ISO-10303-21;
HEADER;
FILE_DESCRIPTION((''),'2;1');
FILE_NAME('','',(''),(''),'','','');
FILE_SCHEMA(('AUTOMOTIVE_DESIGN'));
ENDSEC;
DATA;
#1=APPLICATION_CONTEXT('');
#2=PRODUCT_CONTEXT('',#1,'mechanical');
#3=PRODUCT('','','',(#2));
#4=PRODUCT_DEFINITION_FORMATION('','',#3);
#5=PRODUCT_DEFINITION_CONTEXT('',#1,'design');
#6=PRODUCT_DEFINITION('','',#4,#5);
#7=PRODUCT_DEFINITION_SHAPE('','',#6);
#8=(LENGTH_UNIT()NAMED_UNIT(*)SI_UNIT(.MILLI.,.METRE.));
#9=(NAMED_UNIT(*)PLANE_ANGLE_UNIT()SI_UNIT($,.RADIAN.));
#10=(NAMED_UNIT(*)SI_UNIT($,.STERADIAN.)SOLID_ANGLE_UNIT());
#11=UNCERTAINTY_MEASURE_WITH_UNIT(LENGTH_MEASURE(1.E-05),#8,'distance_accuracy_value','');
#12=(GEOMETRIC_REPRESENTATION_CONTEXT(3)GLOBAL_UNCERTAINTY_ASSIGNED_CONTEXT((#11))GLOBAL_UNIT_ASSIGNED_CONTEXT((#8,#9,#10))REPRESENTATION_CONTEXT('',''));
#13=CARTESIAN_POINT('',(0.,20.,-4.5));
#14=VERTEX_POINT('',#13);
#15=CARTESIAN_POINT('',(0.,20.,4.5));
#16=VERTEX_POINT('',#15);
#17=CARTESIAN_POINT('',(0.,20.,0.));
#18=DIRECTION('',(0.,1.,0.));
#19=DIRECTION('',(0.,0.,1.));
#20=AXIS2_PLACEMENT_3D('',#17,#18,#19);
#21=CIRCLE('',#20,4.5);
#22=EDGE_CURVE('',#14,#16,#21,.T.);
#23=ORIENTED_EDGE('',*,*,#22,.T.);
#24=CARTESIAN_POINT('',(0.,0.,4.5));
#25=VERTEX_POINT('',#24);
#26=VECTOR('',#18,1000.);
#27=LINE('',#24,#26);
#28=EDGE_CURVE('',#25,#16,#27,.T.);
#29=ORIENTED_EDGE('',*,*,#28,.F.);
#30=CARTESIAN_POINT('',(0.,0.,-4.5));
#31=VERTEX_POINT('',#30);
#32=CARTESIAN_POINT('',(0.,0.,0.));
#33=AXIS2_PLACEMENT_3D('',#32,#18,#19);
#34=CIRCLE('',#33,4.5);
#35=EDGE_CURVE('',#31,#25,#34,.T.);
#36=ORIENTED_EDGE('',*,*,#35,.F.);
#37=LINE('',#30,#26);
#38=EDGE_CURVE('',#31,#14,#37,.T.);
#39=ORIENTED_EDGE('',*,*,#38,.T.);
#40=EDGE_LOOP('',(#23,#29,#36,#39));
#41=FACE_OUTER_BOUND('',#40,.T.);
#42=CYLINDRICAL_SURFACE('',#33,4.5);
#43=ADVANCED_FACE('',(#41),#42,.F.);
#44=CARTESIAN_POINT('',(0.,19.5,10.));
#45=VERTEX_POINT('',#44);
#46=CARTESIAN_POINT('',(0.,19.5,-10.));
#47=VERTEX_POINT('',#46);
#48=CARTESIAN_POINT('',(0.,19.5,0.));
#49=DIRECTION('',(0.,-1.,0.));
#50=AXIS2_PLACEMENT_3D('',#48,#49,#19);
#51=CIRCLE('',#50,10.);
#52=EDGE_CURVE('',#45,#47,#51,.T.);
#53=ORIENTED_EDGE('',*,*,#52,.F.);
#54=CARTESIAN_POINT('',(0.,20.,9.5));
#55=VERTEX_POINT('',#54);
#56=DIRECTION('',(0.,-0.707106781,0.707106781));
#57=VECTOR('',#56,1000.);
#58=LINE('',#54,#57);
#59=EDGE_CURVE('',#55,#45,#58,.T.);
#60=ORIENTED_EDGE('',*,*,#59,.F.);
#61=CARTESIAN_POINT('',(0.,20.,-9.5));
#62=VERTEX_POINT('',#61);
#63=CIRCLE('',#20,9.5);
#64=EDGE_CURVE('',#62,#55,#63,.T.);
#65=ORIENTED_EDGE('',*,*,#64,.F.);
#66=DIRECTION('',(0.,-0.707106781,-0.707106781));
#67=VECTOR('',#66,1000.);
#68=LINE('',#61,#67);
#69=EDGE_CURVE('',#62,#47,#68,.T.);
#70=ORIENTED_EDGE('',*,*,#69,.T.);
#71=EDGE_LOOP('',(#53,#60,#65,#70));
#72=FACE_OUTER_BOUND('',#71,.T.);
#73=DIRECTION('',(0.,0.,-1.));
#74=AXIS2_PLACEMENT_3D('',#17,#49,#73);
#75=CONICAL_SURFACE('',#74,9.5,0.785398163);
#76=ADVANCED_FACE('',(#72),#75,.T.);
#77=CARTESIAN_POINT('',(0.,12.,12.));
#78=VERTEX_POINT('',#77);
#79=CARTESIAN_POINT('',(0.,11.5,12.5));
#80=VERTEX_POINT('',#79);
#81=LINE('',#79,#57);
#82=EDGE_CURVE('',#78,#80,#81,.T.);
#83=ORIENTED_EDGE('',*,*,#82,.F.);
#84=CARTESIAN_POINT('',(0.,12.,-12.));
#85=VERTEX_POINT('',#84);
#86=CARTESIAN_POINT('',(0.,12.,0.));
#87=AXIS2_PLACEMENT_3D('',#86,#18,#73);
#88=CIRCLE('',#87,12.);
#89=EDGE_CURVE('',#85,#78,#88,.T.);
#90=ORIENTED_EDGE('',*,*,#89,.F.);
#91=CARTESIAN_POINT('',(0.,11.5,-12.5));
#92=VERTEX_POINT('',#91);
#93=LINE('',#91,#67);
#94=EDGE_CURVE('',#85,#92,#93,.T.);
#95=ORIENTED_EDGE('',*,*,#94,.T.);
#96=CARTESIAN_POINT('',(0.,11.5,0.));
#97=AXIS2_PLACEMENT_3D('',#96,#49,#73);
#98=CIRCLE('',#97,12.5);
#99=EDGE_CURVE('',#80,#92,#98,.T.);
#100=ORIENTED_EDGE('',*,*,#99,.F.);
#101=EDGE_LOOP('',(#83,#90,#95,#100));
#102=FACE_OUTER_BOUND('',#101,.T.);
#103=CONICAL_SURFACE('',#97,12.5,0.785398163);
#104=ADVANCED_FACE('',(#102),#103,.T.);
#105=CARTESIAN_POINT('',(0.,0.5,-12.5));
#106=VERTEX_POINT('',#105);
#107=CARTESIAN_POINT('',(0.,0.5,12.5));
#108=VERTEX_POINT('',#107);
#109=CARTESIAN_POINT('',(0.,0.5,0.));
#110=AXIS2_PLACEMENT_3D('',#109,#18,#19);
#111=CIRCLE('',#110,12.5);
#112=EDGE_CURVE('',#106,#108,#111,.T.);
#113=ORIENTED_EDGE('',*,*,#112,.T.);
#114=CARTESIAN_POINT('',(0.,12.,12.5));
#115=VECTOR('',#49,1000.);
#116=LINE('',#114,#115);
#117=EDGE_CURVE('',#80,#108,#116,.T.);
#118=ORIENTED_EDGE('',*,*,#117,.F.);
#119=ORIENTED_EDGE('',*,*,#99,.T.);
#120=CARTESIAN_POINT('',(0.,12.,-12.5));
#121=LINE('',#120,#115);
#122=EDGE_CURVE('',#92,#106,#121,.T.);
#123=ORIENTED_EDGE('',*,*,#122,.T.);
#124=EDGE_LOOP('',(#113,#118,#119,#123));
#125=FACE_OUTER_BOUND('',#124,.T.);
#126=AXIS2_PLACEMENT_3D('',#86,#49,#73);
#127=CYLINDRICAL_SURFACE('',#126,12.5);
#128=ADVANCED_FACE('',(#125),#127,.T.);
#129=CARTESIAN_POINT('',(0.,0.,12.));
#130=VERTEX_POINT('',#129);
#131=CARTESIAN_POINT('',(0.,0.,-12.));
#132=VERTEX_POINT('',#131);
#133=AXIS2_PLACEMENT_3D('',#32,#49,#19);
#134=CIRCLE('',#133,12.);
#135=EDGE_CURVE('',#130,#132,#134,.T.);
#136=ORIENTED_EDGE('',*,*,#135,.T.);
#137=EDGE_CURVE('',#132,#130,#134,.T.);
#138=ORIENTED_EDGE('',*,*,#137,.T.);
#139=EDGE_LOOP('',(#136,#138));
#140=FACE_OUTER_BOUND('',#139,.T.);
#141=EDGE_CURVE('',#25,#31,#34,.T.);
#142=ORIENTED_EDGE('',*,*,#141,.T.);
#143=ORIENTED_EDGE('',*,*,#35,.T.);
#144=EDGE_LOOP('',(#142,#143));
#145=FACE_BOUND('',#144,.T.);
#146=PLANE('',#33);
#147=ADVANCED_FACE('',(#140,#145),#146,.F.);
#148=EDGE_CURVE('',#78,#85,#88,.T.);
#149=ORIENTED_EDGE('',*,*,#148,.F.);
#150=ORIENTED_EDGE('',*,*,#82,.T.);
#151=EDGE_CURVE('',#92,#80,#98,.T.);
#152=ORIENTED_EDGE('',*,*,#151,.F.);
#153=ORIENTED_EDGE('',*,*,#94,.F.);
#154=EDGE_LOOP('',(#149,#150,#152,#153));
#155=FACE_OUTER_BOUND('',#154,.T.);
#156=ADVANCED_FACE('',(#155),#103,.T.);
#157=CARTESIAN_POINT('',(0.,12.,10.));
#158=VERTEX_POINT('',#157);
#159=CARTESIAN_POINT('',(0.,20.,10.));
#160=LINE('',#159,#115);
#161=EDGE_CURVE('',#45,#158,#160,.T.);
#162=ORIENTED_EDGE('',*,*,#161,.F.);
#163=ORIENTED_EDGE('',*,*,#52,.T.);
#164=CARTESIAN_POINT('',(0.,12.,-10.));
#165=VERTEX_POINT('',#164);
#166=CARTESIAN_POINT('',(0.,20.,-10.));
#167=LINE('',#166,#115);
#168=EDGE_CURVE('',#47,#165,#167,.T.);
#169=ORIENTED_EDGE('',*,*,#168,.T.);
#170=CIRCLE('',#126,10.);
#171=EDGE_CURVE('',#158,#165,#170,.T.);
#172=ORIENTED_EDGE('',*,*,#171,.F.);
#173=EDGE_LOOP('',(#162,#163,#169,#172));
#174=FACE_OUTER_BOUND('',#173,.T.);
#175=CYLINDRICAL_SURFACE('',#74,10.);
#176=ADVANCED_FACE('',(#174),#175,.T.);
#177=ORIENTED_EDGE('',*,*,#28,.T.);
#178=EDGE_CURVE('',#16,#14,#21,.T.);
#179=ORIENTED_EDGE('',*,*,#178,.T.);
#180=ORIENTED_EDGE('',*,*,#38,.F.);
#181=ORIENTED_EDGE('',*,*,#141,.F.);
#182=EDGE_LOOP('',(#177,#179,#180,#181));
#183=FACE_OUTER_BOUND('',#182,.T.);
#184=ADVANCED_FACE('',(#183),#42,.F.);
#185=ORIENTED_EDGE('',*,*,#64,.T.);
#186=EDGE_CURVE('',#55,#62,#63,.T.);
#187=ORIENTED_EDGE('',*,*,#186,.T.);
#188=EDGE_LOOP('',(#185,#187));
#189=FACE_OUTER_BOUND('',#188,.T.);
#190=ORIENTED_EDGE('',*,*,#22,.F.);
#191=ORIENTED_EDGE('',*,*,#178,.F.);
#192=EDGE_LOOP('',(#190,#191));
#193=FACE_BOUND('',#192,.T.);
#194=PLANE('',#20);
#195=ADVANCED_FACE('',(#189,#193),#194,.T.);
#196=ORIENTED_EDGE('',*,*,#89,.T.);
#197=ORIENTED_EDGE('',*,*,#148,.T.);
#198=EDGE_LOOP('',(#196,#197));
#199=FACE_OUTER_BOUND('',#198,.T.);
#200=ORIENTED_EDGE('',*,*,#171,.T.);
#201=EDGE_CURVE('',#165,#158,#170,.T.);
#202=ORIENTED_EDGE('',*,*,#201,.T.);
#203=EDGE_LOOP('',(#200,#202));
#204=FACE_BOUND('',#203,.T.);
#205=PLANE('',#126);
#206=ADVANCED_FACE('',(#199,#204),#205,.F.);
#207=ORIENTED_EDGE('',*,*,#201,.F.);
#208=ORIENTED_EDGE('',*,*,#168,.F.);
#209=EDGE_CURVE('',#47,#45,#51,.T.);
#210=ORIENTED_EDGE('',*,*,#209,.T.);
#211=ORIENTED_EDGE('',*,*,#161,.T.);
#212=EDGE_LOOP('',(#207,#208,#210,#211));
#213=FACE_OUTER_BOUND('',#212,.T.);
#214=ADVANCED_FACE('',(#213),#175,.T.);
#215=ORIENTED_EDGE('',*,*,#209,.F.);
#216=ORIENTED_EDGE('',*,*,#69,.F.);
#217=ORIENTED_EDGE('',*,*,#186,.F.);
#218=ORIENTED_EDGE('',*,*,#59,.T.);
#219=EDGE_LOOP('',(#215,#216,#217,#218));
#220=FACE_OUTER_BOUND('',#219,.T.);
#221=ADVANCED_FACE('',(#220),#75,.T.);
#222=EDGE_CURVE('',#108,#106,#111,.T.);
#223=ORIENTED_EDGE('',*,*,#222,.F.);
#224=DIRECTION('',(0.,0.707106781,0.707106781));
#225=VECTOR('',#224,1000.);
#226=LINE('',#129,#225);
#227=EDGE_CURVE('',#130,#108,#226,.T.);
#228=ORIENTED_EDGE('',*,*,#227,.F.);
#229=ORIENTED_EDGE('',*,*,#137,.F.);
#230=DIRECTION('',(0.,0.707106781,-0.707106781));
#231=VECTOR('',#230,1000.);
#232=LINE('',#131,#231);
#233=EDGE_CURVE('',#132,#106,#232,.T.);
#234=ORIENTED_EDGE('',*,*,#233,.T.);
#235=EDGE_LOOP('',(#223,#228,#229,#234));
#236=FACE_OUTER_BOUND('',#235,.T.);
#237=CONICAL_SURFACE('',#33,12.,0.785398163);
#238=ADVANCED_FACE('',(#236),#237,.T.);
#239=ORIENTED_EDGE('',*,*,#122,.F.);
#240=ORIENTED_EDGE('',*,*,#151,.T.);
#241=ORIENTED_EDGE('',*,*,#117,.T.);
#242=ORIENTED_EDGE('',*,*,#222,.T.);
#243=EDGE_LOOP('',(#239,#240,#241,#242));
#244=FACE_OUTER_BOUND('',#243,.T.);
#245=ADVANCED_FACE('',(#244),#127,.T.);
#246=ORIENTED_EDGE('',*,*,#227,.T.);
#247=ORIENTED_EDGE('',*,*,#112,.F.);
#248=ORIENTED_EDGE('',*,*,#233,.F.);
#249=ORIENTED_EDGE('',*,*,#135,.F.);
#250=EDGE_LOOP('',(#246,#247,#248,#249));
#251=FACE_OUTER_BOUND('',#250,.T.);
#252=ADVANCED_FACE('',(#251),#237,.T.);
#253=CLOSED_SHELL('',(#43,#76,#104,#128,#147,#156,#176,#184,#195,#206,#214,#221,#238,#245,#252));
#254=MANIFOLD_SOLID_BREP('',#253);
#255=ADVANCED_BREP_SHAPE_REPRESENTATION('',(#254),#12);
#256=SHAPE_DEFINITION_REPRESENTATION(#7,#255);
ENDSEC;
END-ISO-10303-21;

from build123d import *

# Parameters (mm, degrees)
SKETCH_1_R          = 10
EXTRUDE_1_DEPTH     = 20
SKETCH_3_R          = 12.5
EXTRUDE_2_DEPTH     = 12
SKETCH_2_R          = 4.5
CUT_EXTRUDE_1_DEPTH = 27.69269563
CHAMFER_2_SIZE      = 0.5


with BuildPart() as part:
    # 草图1 → 凸台-拉伸1 (new body)
    with BuildSketch(Plane(origin=(0, 0, 0), x_dir=(1, 0, 0), z_dir=(0, 1, 0))):
        with Locations(Location((0, 0, 0), (0, 0, 270))):
            Circle(SKETCH_1_R)
    extrude(amount=EXTRUDE_1_DEPTH)

    # 草图3 → 凸台-拉伸2 (add)
    with BuildSketch(Plane(origin=(0, 0, 0), x_dir=(-1, 0, 0), z_dir=(0, -1, 0))):
        with Locations(Location((0, 0, 0), (0, 0, 90))):
            Circle(SKETCH_3_R)
    extrude(amount=-EXTRUDE_2_DEPTH)

    # 草图2 → 切除-拉伸1 (cut, through all)
    with BuildSketch(Plane(origin=(0, 20, 0), x_dir=(1, 0, 0), z_dir=(0, 1, 0))):
        with Locations(Location((0, 0, 0), (0, 0, 270))):
            Circle(SKETCH_2_R)
    extrude(amount=-CUT_EXTRUDE_1_DEPTH, mode=Mode.SUBTRACT)

    # 倒角2
    chamfer_2_edges = [part.edges().sort_by_distance(p)[0] for p in [
        (0, 20, -10),
        (0, 12, 12.5),
        (0, 0, 12.5),
    ]]
    chamfer(chamfer_2_edges, length=CHAMFER_2_SIZE)


solid = part.part
